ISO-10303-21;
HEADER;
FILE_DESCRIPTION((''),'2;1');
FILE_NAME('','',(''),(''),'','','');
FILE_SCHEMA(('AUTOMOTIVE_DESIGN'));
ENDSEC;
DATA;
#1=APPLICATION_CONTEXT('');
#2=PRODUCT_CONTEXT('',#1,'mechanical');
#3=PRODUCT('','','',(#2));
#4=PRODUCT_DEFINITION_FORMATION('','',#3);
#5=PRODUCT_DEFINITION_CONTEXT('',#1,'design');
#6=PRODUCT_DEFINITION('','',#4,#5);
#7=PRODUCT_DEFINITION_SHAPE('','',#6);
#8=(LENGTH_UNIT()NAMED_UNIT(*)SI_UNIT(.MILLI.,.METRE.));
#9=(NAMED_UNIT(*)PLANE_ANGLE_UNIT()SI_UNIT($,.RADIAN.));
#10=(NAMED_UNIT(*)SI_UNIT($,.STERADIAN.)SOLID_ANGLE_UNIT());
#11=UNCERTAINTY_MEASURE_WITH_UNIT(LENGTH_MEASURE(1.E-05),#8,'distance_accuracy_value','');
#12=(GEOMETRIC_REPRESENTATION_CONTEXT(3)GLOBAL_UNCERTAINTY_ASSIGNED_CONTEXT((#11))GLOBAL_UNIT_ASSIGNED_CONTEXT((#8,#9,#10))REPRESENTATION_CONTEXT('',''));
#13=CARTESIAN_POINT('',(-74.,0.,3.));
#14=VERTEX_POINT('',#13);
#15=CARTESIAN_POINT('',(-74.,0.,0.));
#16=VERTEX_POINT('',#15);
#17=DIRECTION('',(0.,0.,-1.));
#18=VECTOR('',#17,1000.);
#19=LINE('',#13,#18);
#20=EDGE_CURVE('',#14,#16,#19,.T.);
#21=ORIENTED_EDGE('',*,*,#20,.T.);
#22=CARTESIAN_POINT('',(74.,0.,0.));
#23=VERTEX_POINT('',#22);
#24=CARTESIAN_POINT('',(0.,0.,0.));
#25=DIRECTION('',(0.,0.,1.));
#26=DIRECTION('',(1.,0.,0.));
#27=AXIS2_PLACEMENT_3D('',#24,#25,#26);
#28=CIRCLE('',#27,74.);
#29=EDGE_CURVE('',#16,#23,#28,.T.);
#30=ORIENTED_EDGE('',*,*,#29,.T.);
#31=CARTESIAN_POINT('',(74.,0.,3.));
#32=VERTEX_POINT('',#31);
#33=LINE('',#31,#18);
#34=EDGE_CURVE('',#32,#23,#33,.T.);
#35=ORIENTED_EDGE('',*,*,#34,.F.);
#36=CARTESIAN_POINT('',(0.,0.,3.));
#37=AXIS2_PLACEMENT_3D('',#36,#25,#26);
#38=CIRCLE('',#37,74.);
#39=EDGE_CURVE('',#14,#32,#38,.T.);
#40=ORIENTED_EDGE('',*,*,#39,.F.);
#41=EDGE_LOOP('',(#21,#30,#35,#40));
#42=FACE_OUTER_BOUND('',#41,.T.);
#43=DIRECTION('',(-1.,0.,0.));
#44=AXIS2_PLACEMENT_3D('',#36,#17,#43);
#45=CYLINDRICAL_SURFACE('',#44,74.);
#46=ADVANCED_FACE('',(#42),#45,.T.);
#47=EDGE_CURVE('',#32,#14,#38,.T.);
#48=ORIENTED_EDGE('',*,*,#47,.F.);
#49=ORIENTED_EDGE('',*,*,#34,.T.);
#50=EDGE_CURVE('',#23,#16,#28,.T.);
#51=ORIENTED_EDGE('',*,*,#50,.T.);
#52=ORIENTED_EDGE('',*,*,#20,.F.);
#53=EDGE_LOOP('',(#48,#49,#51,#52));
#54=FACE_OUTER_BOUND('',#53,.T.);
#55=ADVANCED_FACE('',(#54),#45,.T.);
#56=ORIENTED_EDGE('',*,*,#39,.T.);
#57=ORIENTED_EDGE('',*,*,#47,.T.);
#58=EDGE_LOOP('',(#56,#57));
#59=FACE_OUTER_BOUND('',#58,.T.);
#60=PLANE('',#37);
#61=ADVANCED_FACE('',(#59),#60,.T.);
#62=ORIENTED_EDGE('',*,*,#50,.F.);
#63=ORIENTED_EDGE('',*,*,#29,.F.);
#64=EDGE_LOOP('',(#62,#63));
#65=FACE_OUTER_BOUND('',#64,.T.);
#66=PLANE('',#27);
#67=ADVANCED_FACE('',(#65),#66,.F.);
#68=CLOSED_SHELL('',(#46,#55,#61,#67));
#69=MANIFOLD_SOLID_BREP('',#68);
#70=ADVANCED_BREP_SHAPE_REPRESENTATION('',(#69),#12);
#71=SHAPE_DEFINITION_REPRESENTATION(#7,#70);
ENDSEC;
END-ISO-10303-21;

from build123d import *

# Parameters (mm, degrees)
SKETCH_1_R           = 74
BOSS_EXTRUDE_1_DEPTH = 3


with BuildPart() as part:
    # Sketch 1 → Boss-Extrude 1 (new body)
    with BuildSketch(Plane.XY):
        Circle(SKETCH_1_R)
    extrude(amount=BOSS_EXTRUDE_1_DEPTH)


solid = part.part
